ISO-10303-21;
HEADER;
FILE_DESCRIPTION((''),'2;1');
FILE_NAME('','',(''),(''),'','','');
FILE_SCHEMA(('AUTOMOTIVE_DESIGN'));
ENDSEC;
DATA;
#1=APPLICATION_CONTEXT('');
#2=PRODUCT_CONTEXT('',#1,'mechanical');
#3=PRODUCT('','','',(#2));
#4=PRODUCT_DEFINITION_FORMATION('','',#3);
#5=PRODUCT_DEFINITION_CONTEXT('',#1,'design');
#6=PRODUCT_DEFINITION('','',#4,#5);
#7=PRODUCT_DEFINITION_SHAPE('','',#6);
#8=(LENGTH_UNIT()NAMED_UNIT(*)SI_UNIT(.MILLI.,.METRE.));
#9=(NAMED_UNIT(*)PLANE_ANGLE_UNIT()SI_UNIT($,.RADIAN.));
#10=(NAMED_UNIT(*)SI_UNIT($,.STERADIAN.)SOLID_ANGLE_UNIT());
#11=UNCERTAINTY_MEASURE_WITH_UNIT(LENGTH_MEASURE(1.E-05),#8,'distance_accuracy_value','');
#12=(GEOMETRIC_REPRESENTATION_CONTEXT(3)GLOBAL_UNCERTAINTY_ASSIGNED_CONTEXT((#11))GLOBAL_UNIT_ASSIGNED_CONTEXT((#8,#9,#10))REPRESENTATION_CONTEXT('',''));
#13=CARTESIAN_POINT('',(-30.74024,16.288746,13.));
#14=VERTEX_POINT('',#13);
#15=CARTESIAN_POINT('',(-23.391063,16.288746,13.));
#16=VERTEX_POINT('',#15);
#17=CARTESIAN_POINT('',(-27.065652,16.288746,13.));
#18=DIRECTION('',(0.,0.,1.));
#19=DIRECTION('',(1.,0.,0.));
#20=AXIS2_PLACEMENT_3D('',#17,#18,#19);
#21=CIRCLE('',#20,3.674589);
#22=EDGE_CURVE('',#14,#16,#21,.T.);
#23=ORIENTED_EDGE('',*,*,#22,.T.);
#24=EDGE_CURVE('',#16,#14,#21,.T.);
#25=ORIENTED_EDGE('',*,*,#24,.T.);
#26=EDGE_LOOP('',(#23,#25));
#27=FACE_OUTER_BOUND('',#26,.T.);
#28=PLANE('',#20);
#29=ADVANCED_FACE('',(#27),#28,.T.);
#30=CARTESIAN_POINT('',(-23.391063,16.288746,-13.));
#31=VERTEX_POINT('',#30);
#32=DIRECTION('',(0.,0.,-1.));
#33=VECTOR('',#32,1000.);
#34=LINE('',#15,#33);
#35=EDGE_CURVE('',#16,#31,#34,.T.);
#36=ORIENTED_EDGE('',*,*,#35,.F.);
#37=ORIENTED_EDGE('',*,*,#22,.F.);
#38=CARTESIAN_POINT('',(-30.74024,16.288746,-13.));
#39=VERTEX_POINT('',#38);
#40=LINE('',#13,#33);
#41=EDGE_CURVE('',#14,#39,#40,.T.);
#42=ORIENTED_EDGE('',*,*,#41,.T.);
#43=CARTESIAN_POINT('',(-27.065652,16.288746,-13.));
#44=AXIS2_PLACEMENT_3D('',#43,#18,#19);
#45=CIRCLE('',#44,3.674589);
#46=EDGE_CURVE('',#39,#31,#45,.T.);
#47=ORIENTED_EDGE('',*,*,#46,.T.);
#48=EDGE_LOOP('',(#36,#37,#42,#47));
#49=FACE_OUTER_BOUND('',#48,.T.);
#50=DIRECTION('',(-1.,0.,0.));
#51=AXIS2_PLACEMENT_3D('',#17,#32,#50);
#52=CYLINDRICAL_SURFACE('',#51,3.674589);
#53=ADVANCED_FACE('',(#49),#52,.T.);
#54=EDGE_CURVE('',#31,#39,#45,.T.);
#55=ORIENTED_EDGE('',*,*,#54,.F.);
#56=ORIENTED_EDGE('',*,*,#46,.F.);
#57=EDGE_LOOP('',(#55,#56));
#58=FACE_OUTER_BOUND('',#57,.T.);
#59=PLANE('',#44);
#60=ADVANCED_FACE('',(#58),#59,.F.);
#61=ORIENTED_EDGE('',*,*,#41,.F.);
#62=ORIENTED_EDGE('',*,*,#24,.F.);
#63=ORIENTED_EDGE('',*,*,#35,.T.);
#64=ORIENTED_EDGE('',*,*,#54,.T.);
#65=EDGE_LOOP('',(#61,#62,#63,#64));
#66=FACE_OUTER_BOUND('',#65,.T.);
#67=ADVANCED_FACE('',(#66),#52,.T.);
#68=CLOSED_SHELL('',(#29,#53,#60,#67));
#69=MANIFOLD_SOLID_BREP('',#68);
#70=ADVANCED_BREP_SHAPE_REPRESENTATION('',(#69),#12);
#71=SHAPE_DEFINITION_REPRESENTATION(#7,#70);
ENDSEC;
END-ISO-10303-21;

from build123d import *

# Parameters (mm, degrees)
SKETCH1_R           = 3.674588618
BOSS_EXTRUDE1_DEPTH = 13


with BuildPart() as part:
    # Sketch1 → Boss-Extrude1 (new, symmetric)
    with BuildSketch(Plane.XY):
        with Locations((-27.065651732, 16.288746435)):
            Circle(SKETCH1_R)
    extrude(amount=BOSS_EXTRUDE1_DEPTH, both=True)


solid = part.part
